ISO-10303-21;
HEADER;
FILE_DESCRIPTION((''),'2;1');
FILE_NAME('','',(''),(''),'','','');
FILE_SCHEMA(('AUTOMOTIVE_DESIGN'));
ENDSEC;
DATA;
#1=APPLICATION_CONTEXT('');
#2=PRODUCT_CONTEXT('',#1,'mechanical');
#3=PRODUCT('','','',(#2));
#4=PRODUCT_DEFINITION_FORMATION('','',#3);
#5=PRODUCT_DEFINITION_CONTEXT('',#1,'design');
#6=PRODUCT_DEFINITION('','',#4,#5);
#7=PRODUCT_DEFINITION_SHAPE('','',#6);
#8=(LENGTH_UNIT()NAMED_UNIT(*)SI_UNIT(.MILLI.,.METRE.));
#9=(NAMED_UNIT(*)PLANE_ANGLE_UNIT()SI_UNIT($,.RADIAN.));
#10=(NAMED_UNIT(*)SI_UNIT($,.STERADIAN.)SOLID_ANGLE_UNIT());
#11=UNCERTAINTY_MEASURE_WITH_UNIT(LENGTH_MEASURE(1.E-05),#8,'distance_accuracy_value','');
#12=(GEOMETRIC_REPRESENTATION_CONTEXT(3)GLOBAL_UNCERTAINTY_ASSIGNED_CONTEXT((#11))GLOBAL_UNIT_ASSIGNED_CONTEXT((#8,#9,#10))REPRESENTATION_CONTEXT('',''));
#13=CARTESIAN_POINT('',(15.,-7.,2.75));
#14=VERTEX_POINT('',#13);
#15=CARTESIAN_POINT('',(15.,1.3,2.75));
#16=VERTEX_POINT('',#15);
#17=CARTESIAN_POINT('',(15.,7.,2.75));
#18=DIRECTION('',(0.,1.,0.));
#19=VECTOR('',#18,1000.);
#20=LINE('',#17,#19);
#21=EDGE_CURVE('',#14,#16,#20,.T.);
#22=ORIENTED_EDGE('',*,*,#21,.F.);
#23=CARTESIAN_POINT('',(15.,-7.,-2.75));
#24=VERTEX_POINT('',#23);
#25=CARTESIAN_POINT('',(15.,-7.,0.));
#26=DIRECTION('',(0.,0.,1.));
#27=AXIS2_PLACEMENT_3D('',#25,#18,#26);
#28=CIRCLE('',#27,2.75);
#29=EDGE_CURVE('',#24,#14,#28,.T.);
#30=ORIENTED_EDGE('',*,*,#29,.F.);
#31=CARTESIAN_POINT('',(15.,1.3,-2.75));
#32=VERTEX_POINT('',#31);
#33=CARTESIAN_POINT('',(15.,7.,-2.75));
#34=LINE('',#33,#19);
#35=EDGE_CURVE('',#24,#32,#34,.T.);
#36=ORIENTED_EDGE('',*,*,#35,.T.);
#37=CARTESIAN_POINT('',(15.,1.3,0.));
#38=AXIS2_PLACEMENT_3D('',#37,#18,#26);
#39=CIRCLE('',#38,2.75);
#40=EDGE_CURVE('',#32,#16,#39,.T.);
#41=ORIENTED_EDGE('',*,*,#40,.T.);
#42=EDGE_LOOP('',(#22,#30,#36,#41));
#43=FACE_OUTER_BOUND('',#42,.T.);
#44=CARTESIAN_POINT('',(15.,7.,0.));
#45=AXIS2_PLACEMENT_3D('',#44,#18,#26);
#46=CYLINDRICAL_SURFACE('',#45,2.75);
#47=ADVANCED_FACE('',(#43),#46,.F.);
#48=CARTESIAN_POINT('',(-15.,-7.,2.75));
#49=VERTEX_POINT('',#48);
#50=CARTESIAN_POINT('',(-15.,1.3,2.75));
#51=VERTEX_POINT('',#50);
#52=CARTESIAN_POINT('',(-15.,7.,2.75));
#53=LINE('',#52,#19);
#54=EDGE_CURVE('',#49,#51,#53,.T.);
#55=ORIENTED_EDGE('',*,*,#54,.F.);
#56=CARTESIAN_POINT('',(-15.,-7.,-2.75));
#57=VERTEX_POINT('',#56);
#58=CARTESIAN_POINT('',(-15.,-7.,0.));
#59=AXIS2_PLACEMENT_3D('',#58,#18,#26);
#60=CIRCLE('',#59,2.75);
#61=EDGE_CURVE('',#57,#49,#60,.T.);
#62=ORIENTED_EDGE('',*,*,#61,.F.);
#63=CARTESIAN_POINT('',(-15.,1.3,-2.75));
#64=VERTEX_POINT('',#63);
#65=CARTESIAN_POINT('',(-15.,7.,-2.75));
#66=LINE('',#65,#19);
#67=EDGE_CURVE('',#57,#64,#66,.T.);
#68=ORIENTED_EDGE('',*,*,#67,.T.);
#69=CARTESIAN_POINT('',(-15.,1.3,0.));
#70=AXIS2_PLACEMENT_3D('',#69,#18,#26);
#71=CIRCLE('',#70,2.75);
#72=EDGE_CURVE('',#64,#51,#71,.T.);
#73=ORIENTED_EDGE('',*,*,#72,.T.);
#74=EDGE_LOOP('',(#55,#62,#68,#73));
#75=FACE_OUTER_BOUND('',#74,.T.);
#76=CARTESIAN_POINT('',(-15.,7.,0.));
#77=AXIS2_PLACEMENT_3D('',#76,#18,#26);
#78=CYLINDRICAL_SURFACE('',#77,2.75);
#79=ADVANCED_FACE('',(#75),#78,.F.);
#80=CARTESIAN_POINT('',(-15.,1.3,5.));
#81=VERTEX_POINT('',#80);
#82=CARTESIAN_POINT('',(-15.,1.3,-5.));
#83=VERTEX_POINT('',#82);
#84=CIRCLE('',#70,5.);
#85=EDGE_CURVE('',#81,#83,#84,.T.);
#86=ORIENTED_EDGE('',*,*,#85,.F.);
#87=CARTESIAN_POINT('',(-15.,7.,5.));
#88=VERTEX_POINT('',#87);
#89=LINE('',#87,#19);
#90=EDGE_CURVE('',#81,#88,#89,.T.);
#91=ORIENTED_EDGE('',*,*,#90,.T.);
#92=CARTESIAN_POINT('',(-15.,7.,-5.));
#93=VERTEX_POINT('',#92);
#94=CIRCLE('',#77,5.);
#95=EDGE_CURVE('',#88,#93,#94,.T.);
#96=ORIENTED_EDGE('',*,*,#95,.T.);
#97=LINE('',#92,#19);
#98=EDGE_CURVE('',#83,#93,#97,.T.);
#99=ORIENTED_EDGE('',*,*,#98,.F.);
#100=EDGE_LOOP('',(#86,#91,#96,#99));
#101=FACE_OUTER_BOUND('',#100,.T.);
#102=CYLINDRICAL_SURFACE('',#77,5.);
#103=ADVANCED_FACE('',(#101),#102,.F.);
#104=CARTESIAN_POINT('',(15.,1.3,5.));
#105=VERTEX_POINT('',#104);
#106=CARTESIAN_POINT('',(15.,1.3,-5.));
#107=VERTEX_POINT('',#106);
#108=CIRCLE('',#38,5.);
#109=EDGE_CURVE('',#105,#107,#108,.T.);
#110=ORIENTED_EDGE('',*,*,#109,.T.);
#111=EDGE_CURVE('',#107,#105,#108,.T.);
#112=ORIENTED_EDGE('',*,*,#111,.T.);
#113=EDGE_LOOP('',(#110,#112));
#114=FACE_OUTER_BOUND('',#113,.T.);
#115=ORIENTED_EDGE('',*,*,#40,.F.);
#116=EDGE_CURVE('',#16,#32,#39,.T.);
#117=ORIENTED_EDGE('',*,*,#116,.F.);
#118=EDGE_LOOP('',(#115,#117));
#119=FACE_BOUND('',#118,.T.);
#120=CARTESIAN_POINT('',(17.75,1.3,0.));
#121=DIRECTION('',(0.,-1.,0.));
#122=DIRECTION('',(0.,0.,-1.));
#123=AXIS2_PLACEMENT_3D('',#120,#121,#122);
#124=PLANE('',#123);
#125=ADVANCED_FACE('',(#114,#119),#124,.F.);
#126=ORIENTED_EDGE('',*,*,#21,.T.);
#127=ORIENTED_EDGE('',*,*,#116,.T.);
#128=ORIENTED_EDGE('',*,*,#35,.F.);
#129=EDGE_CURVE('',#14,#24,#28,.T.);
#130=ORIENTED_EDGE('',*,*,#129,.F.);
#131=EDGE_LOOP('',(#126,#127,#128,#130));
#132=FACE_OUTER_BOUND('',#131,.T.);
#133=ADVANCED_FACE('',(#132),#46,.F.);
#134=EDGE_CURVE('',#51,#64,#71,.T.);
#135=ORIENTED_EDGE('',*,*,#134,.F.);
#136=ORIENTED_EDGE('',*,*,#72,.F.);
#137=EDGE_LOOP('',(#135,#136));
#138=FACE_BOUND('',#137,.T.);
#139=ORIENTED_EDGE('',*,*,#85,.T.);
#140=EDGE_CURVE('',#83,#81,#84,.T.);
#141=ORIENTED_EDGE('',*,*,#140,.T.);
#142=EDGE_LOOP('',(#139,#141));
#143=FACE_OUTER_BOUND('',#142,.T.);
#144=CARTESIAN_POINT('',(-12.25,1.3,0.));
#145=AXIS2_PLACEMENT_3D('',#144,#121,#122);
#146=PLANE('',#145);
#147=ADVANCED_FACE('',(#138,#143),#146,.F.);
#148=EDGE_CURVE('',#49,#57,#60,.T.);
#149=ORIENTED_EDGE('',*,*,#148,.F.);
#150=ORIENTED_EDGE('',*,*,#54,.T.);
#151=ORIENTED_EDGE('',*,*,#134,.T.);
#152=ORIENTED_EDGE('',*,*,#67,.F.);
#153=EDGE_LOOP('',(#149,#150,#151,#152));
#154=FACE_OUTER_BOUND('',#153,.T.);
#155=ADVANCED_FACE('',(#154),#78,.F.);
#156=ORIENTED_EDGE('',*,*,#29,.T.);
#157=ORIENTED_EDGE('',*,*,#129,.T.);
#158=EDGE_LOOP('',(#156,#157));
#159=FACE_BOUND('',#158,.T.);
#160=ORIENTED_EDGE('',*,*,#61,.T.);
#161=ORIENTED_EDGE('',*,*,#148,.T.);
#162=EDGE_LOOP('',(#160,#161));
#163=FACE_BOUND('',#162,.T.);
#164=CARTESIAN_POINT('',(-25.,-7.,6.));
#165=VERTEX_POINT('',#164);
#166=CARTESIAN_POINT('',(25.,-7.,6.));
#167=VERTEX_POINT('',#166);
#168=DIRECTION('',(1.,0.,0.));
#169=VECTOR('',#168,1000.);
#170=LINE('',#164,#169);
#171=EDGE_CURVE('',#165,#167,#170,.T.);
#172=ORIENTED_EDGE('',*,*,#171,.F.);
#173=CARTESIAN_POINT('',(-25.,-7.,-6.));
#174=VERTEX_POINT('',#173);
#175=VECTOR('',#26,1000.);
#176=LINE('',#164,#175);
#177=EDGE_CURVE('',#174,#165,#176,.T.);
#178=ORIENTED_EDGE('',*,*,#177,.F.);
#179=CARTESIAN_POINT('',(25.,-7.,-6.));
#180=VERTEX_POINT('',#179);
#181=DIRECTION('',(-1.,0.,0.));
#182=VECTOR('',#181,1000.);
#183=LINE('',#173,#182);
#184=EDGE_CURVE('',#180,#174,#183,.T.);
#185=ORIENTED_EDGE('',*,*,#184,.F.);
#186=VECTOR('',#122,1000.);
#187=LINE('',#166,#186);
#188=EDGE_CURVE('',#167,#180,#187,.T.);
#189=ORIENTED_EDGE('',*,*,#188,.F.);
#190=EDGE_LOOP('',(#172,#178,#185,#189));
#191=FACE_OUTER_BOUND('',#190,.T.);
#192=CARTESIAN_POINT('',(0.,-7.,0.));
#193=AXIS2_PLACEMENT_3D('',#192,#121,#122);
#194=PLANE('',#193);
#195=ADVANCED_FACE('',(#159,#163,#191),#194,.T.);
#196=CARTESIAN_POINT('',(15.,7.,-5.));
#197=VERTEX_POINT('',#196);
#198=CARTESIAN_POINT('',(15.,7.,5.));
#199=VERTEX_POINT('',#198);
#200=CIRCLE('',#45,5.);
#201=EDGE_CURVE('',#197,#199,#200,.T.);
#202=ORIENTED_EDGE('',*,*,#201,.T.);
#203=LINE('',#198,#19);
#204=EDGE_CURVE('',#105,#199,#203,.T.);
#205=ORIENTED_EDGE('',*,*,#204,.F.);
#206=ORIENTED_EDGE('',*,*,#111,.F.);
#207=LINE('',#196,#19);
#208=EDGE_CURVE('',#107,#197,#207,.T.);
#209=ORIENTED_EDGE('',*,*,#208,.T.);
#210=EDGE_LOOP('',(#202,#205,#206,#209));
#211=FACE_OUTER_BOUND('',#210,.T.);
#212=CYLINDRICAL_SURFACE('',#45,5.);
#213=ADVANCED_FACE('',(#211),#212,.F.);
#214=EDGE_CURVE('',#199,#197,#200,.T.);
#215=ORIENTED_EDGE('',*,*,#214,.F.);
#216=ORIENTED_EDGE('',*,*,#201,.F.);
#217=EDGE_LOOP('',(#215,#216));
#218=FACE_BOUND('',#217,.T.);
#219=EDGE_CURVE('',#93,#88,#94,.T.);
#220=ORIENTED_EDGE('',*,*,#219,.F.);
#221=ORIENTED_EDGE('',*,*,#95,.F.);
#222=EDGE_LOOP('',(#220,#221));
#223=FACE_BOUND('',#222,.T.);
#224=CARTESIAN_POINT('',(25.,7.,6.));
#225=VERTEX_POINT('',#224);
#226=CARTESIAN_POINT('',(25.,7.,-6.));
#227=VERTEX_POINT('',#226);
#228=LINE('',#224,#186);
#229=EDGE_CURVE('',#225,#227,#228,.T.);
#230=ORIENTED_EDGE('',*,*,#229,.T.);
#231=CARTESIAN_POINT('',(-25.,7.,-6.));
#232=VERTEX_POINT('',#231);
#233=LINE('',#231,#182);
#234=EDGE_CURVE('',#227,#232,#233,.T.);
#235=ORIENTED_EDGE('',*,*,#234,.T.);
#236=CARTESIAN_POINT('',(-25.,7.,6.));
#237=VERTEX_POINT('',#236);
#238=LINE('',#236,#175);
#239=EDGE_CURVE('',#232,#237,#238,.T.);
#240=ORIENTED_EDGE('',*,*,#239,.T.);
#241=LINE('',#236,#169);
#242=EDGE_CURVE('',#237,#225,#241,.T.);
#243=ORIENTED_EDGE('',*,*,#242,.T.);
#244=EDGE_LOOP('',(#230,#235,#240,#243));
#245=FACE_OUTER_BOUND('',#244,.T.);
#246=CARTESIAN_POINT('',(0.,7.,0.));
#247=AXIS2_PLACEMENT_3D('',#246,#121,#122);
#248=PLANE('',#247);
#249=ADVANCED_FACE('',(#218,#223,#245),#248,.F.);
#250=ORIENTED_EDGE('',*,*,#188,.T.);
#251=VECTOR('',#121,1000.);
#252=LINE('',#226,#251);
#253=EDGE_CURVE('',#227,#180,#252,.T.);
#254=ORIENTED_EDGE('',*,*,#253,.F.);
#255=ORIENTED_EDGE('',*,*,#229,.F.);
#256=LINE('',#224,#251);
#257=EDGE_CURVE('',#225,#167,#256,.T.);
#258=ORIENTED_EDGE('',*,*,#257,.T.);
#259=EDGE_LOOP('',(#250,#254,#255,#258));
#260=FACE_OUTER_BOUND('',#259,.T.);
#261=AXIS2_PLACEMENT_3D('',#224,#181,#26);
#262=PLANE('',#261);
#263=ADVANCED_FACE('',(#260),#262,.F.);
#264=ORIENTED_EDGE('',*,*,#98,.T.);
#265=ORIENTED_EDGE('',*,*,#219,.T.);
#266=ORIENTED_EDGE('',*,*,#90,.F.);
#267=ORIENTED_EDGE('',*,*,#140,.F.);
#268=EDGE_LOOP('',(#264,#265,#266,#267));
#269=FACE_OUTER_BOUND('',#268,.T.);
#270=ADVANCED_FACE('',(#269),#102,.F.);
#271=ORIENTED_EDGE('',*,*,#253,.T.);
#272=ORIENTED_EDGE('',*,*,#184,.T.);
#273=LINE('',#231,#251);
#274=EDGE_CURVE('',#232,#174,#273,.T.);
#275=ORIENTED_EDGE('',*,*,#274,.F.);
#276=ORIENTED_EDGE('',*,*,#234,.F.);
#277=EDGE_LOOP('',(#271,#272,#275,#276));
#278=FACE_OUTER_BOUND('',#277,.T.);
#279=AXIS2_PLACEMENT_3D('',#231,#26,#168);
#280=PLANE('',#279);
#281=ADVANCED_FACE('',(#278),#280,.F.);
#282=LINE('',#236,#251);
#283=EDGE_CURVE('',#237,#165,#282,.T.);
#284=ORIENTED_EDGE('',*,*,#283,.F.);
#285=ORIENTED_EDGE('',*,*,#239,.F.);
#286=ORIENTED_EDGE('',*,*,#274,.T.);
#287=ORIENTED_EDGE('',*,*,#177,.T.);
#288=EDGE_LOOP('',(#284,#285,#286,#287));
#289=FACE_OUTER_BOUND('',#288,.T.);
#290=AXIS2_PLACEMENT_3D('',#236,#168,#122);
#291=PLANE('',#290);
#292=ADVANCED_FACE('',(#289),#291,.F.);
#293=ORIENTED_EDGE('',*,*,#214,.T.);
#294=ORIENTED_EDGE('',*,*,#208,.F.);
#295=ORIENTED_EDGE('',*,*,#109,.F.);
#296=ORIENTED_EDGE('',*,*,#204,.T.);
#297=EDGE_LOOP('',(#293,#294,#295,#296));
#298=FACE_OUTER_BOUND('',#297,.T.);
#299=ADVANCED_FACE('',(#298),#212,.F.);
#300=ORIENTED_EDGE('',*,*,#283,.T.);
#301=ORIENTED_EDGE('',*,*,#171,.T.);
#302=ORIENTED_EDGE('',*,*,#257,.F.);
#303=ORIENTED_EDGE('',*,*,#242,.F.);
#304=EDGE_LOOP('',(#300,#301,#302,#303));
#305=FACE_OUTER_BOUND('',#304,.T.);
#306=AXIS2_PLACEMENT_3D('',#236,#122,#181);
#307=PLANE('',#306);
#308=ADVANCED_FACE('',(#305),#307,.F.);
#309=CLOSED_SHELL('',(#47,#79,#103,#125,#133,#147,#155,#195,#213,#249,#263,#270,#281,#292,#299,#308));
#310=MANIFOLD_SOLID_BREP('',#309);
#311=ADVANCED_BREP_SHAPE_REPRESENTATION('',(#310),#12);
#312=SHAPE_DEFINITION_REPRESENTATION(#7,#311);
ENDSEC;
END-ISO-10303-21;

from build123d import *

# Parameters (mm, degrees)
SKETCH1_W                                           = 50
SKETCH1_H                                           = 12
BOSS_EXTRUDE1_DEPTH                                 = 7
HOLE_SIZE_PER_SOCKET_HEAD_CAP_SCREW_TYP_D           = 5.5
HOLE_SIZE_PER_SOCKET_HEAD_CAP_SCREW_TYP_CBORE_D     = 10
HOLE_SIZE_PER_SOCKET_HEAD_CAP_SCREW_TYP_CBORE_DEPTH = 5.7


with BuildPart() as part:
    # Sketch1 → Boss-Extrude1 (new, symmetric)
    with BuildSketch(Plane(origin=(0, 0, 0), x_dir=(1, 0, 0), z_dir=(0, 1, 0))):
        Rectangle(SKETCH1_W, SKETCH1_H)
    extrude(amount=BOSS_EXTRUDE1_DEPTH, both=True)

    # Hole Size (per socket head cap screw type)1 (through all)
    with Locations(Plane(origin=(0, 7, 0), x_dir=(1, 0, 0), z_dir=(0, 1, 0))):
        with Locations((15, 0), (-15, 0)):
            CounterBoreHole(HOLE_SIZE_PER_SOCKET_HEAD_CAP_SCREW_TYP_D / 2, HOLE_SIZE_PER_SOCKET_HEAD_CAP_SCREW_TYP_CBORE_D / 2, HOLE_SIZE_PER_SOCKET_HEAD_CAP_SCREW_TYP_CBORE_DEPTH)


solid = part.part
